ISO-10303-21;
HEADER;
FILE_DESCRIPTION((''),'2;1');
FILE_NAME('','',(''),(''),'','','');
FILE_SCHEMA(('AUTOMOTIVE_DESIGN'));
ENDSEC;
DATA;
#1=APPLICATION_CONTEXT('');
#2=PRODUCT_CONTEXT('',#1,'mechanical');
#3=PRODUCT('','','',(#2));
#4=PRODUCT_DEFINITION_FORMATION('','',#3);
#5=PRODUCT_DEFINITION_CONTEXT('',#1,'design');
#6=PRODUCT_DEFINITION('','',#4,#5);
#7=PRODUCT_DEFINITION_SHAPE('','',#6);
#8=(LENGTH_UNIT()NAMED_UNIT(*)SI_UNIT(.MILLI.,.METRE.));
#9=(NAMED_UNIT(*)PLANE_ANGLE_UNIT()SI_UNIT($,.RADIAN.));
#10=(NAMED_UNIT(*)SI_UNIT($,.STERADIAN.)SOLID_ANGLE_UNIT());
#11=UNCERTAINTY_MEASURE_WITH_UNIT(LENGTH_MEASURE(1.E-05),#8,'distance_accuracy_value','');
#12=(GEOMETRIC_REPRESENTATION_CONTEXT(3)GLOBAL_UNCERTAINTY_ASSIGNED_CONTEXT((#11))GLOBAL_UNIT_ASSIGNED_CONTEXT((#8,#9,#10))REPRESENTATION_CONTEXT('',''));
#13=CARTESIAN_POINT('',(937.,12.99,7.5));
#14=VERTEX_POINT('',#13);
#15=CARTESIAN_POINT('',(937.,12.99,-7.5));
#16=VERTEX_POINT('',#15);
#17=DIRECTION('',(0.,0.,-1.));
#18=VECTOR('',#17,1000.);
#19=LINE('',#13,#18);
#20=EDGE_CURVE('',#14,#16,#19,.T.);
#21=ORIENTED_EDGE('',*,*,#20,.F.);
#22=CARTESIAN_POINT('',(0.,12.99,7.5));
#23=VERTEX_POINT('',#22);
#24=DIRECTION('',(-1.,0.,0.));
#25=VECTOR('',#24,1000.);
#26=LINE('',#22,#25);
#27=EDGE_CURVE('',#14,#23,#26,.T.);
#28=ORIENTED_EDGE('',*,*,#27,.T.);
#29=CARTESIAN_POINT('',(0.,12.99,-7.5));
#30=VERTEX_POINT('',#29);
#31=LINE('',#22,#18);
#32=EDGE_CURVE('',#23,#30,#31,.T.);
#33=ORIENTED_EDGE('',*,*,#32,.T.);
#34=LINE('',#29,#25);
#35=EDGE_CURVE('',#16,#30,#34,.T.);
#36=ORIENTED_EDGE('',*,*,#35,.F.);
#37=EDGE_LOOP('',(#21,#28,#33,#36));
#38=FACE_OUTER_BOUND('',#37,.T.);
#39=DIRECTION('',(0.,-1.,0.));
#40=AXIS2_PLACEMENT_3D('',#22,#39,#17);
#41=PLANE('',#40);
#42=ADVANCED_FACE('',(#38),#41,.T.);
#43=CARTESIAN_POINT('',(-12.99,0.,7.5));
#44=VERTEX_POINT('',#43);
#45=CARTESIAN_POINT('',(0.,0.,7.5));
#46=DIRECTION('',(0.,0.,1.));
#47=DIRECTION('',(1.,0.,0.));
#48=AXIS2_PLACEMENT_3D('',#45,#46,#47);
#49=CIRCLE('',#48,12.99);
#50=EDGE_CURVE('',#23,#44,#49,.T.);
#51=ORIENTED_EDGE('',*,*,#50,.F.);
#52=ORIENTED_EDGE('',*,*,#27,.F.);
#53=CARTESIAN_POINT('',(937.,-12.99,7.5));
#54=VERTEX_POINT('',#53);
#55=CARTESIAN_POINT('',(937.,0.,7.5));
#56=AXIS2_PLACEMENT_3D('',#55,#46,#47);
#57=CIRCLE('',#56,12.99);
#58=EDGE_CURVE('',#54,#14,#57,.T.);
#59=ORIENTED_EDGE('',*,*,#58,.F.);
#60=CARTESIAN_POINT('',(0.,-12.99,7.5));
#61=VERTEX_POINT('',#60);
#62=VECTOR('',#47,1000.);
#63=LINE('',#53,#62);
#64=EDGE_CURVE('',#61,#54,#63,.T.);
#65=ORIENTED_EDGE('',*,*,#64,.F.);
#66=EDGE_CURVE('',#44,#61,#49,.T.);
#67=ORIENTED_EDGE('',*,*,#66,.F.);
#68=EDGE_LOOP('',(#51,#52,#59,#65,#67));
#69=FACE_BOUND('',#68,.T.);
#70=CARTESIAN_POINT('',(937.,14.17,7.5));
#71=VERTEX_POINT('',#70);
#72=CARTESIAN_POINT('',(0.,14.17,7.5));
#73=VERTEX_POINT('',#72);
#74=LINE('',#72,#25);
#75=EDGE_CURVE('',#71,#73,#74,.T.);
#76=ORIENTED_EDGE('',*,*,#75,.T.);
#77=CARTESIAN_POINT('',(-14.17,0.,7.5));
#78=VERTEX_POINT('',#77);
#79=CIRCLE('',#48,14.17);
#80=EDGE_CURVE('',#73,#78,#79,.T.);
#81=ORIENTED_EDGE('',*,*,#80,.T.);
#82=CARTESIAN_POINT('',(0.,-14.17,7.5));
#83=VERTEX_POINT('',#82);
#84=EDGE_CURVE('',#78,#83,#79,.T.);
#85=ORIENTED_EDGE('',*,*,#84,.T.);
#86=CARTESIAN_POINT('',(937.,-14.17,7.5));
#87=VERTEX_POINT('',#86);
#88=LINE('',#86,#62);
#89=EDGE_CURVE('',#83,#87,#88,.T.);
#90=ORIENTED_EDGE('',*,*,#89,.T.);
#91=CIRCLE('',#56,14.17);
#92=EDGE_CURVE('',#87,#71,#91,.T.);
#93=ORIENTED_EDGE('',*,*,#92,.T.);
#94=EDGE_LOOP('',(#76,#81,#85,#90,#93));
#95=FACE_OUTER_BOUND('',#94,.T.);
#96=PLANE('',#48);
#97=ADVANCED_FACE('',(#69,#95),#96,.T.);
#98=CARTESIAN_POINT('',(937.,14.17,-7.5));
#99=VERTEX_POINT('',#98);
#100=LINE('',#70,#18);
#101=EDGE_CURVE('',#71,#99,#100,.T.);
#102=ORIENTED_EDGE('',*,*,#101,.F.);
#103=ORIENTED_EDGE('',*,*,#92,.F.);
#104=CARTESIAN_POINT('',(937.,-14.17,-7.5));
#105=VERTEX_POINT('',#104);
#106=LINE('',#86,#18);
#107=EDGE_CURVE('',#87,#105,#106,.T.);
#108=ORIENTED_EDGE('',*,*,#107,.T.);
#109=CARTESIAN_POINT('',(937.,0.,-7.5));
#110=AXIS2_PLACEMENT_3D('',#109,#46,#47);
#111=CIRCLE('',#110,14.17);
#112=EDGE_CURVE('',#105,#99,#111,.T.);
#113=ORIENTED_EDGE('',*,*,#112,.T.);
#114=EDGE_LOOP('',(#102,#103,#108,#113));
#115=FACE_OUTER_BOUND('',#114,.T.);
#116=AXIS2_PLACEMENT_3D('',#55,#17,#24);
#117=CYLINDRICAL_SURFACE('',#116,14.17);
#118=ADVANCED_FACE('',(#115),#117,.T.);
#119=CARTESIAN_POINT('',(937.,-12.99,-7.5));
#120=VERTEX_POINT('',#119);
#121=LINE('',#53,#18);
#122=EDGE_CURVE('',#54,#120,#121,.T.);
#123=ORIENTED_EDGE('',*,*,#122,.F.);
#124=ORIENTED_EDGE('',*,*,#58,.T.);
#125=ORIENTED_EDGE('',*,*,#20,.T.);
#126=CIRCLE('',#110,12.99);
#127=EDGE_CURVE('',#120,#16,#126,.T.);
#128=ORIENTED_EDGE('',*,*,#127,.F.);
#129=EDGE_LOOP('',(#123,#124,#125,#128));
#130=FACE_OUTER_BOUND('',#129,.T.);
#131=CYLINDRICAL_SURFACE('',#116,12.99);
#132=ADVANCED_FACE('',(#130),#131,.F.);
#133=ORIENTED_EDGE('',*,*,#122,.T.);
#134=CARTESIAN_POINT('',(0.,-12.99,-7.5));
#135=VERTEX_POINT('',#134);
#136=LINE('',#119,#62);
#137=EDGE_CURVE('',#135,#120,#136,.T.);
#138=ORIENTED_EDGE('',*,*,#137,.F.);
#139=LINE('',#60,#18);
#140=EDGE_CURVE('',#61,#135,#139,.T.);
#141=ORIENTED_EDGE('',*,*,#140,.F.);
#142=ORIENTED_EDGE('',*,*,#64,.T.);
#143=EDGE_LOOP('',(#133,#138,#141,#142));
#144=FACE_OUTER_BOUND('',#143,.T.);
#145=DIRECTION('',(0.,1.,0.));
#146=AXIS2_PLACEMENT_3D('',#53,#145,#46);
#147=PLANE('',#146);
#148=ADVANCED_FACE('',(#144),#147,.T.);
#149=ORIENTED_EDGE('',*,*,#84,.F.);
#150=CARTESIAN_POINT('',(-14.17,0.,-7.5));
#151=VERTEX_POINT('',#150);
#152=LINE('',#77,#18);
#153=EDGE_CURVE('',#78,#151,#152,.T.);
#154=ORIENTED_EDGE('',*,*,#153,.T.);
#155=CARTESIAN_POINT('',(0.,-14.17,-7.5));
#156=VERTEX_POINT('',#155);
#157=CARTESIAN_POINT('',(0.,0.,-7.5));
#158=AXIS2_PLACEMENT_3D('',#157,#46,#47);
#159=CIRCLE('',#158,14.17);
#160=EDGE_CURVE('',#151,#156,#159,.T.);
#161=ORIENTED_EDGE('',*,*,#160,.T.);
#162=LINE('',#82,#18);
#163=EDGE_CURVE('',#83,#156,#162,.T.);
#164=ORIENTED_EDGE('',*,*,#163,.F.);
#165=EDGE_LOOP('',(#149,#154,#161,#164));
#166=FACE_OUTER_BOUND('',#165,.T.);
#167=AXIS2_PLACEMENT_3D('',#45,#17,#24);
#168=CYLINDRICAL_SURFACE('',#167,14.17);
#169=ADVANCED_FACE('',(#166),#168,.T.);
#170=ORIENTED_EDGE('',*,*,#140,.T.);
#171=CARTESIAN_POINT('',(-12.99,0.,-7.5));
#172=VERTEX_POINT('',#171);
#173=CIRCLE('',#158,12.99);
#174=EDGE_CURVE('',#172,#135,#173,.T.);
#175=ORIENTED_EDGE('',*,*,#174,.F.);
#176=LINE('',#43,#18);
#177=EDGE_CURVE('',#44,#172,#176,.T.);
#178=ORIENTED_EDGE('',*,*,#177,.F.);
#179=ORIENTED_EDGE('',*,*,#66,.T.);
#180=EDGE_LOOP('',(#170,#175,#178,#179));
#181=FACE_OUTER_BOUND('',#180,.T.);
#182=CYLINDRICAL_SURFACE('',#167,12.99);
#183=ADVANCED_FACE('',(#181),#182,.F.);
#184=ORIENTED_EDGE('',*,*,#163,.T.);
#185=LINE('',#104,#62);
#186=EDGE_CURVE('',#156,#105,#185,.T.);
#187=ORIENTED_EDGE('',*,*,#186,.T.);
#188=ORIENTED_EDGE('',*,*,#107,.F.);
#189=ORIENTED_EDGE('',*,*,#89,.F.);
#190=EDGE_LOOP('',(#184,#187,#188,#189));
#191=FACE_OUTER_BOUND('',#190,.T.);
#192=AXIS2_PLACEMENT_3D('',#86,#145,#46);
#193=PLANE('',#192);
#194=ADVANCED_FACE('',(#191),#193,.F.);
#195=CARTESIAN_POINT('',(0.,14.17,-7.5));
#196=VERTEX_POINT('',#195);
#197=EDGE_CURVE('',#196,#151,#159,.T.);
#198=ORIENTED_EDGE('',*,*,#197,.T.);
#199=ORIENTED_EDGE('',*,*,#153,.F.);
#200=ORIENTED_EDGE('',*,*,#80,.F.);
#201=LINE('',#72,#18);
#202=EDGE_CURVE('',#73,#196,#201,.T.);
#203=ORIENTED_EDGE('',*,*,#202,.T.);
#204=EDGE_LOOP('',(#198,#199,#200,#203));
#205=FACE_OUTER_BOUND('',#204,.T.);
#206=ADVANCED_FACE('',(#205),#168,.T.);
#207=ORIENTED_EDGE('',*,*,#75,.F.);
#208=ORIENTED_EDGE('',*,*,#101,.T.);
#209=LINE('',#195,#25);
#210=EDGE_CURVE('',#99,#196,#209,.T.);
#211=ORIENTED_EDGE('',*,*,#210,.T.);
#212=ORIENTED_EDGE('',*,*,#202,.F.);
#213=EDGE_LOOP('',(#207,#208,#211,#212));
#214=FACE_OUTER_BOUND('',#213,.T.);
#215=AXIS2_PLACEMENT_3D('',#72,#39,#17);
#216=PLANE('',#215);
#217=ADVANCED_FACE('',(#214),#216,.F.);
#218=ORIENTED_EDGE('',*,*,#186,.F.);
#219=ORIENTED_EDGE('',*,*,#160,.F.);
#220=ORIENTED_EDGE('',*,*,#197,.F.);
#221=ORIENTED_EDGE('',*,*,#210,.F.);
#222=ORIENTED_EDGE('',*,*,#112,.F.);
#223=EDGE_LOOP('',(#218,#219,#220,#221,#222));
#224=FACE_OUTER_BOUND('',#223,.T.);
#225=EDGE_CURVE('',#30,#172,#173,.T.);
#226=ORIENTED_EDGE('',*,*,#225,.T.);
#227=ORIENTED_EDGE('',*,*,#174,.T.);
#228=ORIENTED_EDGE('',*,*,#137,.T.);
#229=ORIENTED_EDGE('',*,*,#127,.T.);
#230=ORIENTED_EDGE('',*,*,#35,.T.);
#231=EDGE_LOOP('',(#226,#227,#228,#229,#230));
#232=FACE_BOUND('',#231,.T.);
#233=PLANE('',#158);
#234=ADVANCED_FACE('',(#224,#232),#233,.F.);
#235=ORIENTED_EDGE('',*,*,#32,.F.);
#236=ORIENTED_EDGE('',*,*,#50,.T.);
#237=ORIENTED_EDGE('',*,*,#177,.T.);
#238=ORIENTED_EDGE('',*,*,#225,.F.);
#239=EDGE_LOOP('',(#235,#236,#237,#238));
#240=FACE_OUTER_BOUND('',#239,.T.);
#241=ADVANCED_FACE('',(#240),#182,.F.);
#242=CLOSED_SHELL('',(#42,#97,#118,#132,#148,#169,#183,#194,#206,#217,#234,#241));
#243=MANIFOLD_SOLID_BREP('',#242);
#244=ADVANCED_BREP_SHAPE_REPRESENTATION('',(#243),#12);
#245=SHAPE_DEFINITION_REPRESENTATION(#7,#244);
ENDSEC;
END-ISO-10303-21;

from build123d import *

# Parameters (mm, degrees)
EXTRUDE_1_DEPTH = 7.5


with BuildPart() as part:
    # 草图1 → 凸台-拉伸1 (new, symmetric)
    with BuildSketch(Plane.XY):
        with BuildLine():
            Line((0, 14.17), (937, 14.17))
            ThreePointArc((937, 14.17), (951.17, 0), (937, -14.17))
            Line((937, -14.17), (0, -14.17))
            ThreePointArc((0, -14.17), (-14.17, 0), (0, 14.17))
        make_face()
        with BuildLine():
            Line((0, 12.99), (937, 12.99))
            ThreePointArc((937, 12.99), (949.99, 0), (937, -12.99))
            Line((937, -12.99), (0, -12.99))
            ThreePointArc((0, -12.99), (-12.99, 0), (0, 12.99))
        make_face(mode=Mode.SUBTRACT)
    extrude(amount=EXTRUDE_1_DEPTH, both=True)


solid = part.part
